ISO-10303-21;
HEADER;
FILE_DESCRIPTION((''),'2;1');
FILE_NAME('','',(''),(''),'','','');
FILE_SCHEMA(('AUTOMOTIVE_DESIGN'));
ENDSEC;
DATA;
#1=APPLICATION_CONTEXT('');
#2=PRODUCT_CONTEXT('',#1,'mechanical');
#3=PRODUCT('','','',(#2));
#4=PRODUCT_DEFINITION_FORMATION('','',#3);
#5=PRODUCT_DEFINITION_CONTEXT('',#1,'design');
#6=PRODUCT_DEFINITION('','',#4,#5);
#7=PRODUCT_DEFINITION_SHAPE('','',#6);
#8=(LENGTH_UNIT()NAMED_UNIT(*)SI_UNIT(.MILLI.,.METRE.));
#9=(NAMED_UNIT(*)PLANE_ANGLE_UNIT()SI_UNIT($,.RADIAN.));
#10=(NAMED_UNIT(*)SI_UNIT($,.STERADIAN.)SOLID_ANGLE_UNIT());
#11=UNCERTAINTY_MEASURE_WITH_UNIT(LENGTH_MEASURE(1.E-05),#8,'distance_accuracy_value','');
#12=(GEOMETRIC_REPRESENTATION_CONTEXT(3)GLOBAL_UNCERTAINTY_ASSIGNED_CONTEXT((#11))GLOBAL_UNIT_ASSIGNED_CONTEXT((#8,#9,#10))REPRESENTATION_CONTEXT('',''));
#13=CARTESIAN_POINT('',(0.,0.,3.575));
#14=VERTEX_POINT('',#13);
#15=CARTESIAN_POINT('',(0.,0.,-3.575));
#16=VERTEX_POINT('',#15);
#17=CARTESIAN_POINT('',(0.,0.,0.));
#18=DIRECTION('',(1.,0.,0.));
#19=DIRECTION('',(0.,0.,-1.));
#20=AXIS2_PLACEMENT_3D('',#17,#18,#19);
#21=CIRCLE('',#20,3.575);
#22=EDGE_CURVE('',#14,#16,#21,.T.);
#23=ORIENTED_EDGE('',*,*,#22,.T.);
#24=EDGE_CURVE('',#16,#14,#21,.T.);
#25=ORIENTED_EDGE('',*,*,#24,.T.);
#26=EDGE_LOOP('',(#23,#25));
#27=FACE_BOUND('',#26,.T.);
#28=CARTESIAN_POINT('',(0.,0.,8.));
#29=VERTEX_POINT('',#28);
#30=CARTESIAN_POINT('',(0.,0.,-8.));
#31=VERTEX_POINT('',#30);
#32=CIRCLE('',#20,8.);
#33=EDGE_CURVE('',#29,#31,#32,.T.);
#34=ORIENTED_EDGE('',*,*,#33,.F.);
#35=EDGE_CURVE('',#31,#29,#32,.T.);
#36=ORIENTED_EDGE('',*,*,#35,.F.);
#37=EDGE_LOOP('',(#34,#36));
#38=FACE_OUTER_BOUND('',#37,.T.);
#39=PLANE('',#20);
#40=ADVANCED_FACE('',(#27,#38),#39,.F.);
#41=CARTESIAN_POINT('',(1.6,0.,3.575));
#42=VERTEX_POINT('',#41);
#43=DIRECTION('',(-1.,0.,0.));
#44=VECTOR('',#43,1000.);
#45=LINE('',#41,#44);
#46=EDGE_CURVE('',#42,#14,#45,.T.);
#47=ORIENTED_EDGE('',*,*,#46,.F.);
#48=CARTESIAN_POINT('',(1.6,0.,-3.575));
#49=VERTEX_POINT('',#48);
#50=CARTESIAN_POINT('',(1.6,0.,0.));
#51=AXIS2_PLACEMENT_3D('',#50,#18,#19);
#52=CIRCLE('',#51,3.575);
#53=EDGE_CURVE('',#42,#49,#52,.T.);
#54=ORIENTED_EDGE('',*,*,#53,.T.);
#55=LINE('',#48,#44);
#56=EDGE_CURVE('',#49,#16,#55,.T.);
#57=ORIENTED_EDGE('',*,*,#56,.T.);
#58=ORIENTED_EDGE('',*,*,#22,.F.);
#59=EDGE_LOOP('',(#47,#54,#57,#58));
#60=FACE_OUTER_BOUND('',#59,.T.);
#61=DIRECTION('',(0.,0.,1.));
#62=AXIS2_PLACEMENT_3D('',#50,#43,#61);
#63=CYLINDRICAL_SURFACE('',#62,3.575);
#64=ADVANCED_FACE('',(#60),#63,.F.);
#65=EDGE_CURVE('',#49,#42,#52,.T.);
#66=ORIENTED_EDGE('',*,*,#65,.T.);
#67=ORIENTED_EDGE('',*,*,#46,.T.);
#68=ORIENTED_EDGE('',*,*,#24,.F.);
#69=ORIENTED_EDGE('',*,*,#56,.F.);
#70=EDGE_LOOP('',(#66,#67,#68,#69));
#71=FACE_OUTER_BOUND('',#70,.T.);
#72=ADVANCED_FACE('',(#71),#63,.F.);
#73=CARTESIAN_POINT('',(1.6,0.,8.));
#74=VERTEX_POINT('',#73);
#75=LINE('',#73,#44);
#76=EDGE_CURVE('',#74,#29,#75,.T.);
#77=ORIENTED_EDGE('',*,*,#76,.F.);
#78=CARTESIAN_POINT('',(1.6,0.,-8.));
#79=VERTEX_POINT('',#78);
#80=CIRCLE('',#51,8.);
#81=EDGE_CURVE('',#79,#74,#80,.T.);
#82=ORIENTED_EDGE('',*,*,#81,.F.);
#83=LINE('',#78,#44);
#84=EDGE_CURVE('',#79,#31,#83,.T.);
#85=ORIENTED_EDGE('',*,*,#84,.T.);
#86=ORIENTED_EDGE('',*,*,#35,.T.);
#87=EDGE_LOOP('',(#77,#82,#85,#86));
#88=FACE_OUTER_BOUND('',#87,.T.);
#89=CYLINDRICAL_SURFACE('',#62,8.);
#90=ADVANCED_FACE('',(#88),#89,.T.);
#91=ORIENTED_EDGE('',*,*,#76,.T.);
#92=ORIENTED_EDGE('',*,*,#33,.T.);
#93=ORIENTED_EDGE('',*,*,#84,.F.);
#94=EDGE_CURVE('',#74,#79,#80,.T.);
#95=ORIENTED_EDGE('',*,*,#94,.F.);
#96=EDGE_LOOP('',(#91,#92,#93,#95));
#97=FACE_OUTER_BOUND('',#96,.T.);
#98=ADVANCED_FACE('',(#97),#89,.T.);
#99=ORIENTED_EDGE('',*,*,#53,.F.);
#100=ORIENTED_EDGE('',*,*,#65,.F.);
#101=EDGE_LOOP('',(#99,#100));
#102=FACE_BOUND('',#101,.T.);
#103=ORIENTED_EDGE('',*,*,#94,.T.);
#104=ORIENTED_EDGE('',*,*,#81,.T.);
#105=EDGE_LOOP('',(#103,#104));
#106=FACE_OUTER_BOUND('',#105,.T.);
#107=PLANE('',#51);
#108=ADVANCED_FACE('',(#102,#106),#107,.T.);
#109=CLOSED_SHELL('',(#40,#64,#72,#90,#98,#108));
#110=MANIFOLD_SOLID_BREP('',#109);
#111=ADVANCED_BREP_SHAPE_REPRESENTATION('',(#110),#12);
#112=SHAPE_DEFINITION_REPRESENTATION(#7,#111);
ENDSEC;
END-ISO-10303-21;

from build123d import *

# Parameters (mm, degrees)
SKETCH1_R          = 8
SKETCH1_R_2        = 3.575
BASE_EXTRUDE_DEPTH = 1.6


with BuildPart() as part:
    # Sketch1 → Base-Extrude (new body)
    with BuildSketch(Plane(origin=(0, 0, 0), x_dir=(0, 0, -1), z_dir=(1, 0, 0))):
        Circle(SKETCH1_R)
        Circle(SKETCH1_R_2, mode=Mode.SUBTRACT)
    extrude(amount=BASE_EXTRUDE_DEPTH)


solid = part.part
